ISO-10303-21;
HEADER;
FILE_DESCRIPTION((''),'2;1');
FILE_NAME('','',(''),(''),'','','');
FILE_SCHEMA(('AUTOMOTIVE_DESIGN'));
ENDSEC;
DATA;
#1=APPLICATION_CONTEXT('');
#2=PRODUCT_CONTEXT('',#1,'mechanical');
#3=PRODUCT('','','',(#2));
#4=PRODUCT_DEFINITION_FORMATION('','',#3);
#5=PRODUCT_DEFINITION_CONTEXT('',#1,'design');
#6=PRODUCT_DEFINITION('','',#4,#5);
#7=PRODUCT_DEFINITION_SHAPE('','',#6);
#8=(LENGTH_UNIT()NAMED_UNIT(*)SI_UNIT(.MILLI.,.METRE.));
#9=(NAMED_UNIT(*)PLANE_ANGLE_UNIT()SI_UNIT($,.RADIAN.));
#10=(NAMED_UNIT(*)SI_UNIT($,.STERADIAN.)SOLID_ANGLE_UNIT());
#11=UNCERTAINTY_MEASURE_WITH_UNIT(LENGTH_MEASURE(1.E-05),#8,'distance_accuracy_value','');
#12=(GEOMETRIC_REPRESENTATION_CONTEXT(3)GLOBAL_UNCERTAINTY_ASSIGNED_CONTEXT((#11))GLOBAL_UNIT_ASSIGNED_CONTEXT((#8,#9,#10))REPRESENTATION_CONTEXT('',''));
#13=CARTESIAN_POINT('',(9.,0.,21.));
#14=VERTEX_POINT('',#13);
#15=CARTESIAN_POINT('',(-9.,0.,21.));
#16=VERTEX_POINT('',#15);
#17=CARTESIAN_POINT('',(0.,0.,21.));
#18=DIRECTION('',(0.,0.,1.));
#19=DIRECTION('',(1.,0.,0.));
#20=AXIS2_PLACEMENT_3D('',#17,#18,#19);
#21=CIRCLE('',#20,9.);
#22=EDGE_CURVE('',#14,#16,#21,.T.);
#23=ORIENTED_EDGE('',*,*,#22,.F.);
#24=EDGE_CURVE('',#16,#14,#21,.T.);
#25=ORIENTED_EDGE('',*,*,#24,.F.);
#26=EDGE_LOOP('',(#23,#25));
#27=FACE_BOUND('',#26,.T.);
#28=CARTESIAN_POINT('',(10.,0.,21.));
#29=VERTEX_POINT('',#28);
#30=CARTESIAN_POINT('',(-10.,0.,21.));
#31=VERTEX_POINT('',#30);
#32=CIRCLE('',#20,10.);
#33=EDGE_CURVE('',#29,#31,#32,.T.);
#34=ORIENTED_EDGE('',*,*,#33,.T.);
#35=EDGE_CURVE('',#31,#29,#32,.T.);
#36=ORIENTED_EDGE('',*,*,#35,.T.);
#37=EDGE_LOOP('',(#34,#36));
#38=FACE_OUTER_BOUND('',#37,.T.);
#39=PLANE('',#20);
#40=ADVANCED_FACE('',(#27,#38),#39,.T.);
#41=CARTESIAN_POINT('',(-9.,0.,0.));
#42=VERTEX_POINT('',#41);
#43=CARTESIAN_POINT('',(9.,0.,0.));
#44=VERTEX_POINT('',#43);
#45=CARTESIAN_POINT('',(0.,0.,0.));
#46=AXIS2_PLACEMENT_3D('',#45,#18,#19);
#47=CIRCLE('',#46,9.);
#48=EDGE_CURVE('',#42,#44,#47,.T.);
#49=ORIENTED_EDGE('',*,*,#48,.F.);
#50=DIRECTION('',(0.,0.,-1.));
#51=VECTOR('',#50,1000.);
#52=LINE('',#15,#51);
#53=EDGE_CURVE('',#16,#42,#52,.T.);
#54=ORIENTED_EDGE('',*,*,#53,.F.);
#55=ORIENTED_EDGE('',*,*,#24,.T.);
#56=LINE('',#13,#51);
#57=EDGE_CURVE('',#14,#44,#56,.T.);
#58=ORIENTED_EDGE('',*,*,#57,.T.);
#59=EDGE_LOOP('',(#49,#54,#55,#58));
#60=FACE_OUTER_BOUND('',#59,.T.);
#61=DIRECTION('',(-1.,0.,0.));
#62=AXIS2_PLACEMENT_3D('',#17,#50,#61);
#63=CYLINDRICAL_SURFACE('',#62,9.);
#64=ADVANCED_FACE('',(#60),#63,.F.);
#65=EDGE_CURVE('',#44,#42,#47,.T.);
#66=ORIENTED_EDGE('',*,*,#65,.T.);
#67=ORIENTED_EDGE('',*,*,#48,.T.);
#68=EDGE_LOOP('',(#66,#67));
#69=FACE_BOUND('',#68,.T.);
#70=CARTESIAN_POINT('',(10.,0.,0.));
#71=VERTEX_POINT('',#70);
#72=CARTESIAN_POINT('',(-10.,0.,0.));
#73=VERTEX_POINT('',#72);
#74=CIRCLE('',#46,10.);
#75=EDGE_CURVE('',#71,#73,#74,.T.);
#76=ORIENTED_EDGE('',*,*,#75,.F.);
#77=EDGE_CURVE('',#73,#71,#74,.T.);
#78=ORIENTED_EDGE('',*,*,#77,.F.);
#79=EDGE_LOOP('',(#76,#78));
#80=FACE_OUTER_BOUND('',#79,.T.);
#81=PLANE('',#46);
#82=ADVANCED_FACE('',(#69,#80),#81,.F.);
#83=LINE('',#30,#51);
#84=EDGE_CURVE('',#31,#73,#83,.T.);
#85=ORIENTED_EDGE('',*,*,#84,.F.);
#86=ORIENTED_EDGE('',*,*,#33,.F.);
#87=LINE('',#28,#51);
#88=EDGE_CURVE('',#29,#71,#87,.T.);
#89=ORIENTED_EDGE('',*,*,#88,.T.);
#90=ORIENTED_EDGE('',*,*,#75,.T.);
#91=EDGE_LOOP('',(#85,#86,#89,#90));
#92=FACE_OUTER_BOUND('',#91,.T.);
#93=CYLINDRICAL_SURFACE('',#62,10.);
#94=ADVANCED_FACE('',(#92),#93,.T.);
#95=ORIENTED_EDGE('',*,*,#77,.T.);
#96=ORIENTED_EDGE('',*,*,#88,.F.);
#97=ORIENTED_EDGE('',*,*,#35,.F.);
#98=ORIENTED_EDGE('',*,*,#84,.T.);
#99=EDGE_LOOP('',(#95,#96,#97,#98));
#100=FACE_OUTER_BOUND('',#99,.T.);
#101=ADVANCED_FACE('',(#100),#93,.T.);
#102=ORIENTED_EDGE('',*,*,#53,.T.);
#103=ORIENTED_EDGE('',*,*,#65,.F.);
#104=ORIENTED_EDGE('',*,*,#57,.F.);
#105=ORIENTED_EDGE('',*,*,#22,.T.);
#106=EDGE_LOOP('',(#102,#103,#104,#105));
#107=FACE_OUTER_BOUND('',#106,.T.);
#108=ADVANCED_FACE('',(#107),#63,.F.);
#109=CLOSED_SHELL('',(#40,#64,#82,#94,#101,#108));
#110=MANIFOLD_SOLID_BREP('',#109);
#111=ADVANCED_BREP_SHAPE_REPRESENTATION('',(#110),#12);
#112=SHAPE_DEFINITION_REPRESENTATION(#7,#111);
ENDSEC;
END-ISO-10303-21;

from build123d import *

# Parameters (mm, degrees)
SKETCH1_R           = 10
SKETCH1_R_2         = 9
BOSS_EXTRUDE1_DEPTH = 21


with BuildPart() as part:
    # Sketch1 → Boss-Extrude1 (new body)
    with BuildSketch(Plane.XY):
        with Locations(Location((0, 0, 0), (0, 0, 180))):
            Circle(SKETCH1_R)
        with Locations(Location((0, 0, 0), (0, 0, 180))):
            Circle(SKETCH1_R_2, mode=Mode.SUBTRACT)
    extrude(amount=BOSS_EXTRUDE1_DEPTH)


solid = part.part
